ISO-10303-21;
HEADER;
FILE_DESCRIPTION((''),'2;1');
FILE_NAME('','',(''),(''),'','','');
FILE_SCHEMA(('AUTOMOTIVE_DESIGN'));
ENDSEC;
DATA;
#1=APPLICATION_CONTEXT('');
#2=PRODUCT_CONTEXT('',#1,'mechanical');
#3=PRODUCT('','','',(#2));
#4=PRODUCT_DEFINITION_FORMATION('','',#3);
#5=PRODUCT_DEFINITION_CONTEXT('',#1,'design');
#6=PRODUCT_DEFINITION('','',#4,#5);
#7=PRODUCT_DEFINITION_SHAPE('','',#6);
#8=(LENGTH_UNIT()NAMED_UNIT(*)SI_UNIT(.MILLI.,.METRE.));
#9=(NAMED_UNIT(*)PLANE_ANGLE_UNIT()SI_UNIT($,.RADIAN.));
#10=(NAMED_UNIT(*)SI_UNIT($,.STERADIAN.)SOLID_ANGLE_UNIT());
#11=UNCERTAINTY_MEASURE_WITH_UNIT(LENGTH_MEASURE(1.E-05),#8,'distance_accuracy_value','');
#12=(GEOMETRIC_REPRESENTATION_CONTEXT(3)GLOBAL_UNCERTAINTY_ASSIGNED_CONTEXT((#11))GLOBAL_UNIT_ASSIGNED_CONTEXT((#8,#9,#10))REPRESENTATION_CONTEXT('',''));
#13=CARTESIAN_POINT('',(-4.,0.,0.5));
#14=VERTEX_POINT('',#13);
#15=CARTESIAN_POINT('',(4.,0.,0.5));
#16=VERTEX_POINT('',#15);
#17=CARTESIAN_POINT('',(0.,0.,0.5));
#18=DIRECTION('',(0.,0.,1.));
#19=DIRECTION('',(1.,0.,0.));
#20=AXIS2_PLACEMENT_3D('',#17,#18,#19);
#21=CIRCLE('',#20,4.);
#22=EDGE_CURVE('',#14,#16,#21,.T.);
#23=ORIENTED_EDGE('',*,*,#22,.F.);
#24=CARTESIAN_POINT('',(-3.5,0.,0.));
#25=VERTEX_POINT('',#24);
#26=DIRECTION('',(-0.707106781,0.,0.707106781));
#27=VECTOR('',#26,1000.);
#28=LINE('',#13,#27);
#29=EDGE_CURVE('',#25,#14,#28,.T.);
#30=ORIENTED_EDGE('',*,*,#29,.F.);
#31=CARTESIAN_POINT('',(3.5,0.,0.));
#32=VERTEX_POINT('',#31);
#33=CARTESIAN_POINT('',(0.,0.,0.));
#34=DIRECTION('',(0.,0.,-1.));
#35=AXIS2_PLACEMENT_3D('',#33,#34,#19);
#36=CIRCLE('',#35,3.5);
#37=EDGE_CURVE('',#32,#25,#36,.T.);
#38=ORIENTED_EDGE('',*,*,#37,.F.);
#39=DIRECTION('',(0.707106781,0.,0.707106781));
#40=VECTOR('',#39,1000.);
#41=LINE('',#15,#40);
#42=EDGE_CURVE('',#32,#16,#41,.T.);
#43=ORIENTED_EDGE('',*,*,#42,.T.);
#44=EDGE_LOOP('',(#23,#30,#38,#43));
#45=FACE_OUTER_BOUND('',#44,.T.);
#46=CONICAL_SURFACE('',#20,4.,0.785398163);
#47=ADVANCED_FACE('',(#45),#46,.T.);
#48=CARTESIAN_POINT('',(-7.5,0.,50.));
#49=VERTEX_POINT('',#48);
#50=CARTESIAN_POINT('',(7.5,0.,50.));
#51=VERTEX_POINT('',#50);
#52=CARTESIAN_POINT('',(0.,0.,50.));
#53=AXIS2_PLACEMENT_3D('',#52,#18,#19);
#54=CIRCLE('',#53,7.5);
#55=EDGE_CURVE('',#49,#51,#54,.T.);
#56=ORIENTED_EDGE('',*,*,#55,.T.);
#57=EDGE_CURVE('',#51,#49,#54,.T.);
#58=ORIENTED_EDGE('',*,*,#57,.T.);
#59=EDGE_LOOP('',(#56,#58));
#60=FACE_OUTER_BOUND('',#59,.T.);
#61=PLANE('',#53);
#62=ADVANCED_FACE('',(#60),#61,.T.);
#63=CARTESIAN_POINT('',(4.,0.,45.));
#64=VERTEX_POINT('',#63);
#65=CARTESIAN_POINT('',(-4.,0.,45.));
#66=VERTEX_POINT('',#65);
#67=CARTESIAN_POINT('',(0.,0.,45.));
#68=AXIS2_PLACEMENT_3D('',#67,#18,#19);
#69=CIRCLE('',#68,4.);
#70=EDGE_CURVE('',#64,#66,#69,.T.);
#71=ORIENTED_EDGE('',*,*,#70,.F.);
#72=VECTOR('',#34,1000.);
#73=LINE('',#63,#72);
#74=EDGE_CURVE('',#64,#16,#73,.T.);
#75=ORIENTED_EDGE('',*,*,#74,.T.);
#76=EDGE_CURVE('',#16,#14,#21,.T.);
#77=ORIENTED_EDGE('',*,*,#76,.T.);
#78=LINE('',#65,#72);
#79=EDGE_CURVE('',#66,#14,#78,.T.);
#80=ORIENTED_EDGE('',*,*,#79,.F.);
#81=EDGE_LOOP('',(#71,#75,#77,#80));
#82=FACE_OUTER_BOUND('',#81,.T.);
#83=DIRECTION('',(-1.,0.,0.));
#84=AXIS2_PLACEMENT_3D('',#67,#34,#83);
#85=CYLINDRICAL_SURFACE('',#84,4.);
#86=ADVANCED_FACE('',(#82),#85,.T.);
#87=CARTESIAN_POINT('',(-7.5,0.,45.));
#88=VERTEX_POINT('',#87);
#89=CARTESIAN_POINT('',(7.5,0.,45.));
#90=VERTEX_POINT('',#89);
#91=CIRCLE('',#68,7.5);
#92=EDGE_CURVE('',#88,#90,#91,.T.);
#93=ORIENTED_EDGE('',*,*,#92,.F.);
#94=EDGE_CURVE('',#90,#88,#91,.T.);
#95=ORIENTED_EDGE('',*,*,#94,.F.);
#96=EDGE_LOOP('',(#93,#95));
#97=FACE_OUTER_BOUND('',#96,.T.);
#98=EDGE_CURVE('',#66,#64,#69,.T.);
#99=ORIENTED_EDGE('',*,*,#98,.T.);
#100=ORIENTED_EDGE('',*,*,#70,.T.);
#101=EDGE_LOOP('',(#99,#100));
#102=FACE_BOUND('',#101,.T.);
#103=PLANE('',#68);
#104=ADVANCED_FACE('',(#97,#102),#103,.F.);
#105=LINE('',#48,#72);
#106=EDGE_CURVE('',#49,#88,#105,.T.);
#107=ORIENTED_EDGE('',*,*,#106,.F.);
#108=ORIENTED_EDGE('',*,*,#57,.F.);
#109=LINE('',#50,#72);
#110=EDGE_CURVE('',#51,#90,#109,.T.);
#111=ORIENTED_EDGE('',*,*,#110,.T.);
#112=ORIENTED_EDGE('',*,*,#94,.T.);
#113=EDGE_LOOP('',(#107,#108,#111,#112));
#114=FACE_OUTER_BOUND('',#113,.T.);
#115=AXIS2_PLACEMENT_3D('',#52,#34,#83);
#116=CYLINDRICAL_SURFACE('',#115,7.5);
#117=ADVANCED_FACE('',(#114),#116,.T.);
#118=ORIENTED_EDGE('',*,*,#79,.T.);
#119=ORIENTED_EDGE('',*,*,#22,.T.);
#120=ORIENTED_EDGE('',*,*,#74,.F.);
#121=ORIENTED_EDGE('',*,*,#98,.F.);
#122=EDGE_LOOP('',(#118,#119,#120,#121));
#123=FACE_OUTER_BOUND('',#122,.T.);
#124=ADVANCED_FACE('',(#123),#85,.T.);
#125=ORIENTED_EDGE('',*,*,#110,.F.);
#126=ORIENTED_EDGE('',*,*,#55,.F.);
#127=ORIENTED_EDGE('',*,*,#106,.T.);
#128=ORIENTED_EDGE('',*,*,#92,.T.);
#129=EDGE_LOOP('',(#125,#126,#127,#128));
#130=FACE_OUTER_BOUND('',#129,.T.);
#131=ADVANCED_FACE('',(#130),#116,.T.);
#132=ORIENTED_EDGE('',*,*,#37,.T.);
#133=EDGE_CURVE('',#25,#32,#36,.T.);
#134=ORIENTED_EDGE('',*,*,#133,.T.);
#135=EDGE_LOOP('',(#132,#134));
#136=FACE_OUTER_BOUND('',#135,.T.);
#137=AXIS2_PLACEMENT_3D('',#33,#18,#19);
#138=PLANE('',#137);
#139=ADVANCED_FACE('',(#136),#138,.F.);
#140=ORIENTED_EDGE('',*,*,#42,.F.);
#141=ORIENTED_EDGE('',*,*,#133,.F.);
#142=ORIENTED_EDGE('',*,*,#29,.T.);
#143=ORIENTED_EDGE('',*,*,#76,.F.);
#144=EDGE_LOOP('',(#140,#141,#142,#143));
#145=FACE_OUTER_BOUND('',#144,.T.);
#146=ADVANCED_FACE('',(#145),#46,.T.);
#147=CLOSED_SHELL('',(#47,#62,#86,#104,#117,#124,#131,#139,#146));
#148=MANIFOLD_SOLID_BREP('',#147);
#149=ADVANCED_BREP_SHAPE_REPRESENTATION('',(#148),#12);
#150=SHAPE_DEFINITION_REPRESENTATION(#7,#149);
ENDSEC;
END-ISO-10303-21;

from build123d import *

# Parameters (mm, degrees)
SKETCH1_R           = 4
BOSS_EXTRUDE1_DEPTH = 45
SKETCH2_R           = 7.5
BOSS_EXTRUDE2_DEPTH = 5
CHAMFER1_SIZE       = 0.5


with BuildPart() as part:
    # Sketch1 → Boss-Extrude1 (new body)
    with BuildSketch(Plane.XY):
        with Locations(Location((0, 0, 0), (0, 0, 180))):
            Circle(SKETCH1_R)
    extrude(amount=BOSS_EXTRUDE1_DEPTH)

    # Sketch2 → Boss-Extrude2 (add)
    with BuildSketch(Plane.XY.offset(45)):
        Circle(SKETCH2_R)
    extrude(amount=BOSS_EXTRUDE2_DEPTH)

    # Chamfer1
    chamfer1_edges = [part.edges().sort_by_distance(p)[0] for p in [
        (4, 0, 0),
    ]]
    chamfer(chamfer1_edges, length=CHAMFER1_SIZE)


solid = part.part
